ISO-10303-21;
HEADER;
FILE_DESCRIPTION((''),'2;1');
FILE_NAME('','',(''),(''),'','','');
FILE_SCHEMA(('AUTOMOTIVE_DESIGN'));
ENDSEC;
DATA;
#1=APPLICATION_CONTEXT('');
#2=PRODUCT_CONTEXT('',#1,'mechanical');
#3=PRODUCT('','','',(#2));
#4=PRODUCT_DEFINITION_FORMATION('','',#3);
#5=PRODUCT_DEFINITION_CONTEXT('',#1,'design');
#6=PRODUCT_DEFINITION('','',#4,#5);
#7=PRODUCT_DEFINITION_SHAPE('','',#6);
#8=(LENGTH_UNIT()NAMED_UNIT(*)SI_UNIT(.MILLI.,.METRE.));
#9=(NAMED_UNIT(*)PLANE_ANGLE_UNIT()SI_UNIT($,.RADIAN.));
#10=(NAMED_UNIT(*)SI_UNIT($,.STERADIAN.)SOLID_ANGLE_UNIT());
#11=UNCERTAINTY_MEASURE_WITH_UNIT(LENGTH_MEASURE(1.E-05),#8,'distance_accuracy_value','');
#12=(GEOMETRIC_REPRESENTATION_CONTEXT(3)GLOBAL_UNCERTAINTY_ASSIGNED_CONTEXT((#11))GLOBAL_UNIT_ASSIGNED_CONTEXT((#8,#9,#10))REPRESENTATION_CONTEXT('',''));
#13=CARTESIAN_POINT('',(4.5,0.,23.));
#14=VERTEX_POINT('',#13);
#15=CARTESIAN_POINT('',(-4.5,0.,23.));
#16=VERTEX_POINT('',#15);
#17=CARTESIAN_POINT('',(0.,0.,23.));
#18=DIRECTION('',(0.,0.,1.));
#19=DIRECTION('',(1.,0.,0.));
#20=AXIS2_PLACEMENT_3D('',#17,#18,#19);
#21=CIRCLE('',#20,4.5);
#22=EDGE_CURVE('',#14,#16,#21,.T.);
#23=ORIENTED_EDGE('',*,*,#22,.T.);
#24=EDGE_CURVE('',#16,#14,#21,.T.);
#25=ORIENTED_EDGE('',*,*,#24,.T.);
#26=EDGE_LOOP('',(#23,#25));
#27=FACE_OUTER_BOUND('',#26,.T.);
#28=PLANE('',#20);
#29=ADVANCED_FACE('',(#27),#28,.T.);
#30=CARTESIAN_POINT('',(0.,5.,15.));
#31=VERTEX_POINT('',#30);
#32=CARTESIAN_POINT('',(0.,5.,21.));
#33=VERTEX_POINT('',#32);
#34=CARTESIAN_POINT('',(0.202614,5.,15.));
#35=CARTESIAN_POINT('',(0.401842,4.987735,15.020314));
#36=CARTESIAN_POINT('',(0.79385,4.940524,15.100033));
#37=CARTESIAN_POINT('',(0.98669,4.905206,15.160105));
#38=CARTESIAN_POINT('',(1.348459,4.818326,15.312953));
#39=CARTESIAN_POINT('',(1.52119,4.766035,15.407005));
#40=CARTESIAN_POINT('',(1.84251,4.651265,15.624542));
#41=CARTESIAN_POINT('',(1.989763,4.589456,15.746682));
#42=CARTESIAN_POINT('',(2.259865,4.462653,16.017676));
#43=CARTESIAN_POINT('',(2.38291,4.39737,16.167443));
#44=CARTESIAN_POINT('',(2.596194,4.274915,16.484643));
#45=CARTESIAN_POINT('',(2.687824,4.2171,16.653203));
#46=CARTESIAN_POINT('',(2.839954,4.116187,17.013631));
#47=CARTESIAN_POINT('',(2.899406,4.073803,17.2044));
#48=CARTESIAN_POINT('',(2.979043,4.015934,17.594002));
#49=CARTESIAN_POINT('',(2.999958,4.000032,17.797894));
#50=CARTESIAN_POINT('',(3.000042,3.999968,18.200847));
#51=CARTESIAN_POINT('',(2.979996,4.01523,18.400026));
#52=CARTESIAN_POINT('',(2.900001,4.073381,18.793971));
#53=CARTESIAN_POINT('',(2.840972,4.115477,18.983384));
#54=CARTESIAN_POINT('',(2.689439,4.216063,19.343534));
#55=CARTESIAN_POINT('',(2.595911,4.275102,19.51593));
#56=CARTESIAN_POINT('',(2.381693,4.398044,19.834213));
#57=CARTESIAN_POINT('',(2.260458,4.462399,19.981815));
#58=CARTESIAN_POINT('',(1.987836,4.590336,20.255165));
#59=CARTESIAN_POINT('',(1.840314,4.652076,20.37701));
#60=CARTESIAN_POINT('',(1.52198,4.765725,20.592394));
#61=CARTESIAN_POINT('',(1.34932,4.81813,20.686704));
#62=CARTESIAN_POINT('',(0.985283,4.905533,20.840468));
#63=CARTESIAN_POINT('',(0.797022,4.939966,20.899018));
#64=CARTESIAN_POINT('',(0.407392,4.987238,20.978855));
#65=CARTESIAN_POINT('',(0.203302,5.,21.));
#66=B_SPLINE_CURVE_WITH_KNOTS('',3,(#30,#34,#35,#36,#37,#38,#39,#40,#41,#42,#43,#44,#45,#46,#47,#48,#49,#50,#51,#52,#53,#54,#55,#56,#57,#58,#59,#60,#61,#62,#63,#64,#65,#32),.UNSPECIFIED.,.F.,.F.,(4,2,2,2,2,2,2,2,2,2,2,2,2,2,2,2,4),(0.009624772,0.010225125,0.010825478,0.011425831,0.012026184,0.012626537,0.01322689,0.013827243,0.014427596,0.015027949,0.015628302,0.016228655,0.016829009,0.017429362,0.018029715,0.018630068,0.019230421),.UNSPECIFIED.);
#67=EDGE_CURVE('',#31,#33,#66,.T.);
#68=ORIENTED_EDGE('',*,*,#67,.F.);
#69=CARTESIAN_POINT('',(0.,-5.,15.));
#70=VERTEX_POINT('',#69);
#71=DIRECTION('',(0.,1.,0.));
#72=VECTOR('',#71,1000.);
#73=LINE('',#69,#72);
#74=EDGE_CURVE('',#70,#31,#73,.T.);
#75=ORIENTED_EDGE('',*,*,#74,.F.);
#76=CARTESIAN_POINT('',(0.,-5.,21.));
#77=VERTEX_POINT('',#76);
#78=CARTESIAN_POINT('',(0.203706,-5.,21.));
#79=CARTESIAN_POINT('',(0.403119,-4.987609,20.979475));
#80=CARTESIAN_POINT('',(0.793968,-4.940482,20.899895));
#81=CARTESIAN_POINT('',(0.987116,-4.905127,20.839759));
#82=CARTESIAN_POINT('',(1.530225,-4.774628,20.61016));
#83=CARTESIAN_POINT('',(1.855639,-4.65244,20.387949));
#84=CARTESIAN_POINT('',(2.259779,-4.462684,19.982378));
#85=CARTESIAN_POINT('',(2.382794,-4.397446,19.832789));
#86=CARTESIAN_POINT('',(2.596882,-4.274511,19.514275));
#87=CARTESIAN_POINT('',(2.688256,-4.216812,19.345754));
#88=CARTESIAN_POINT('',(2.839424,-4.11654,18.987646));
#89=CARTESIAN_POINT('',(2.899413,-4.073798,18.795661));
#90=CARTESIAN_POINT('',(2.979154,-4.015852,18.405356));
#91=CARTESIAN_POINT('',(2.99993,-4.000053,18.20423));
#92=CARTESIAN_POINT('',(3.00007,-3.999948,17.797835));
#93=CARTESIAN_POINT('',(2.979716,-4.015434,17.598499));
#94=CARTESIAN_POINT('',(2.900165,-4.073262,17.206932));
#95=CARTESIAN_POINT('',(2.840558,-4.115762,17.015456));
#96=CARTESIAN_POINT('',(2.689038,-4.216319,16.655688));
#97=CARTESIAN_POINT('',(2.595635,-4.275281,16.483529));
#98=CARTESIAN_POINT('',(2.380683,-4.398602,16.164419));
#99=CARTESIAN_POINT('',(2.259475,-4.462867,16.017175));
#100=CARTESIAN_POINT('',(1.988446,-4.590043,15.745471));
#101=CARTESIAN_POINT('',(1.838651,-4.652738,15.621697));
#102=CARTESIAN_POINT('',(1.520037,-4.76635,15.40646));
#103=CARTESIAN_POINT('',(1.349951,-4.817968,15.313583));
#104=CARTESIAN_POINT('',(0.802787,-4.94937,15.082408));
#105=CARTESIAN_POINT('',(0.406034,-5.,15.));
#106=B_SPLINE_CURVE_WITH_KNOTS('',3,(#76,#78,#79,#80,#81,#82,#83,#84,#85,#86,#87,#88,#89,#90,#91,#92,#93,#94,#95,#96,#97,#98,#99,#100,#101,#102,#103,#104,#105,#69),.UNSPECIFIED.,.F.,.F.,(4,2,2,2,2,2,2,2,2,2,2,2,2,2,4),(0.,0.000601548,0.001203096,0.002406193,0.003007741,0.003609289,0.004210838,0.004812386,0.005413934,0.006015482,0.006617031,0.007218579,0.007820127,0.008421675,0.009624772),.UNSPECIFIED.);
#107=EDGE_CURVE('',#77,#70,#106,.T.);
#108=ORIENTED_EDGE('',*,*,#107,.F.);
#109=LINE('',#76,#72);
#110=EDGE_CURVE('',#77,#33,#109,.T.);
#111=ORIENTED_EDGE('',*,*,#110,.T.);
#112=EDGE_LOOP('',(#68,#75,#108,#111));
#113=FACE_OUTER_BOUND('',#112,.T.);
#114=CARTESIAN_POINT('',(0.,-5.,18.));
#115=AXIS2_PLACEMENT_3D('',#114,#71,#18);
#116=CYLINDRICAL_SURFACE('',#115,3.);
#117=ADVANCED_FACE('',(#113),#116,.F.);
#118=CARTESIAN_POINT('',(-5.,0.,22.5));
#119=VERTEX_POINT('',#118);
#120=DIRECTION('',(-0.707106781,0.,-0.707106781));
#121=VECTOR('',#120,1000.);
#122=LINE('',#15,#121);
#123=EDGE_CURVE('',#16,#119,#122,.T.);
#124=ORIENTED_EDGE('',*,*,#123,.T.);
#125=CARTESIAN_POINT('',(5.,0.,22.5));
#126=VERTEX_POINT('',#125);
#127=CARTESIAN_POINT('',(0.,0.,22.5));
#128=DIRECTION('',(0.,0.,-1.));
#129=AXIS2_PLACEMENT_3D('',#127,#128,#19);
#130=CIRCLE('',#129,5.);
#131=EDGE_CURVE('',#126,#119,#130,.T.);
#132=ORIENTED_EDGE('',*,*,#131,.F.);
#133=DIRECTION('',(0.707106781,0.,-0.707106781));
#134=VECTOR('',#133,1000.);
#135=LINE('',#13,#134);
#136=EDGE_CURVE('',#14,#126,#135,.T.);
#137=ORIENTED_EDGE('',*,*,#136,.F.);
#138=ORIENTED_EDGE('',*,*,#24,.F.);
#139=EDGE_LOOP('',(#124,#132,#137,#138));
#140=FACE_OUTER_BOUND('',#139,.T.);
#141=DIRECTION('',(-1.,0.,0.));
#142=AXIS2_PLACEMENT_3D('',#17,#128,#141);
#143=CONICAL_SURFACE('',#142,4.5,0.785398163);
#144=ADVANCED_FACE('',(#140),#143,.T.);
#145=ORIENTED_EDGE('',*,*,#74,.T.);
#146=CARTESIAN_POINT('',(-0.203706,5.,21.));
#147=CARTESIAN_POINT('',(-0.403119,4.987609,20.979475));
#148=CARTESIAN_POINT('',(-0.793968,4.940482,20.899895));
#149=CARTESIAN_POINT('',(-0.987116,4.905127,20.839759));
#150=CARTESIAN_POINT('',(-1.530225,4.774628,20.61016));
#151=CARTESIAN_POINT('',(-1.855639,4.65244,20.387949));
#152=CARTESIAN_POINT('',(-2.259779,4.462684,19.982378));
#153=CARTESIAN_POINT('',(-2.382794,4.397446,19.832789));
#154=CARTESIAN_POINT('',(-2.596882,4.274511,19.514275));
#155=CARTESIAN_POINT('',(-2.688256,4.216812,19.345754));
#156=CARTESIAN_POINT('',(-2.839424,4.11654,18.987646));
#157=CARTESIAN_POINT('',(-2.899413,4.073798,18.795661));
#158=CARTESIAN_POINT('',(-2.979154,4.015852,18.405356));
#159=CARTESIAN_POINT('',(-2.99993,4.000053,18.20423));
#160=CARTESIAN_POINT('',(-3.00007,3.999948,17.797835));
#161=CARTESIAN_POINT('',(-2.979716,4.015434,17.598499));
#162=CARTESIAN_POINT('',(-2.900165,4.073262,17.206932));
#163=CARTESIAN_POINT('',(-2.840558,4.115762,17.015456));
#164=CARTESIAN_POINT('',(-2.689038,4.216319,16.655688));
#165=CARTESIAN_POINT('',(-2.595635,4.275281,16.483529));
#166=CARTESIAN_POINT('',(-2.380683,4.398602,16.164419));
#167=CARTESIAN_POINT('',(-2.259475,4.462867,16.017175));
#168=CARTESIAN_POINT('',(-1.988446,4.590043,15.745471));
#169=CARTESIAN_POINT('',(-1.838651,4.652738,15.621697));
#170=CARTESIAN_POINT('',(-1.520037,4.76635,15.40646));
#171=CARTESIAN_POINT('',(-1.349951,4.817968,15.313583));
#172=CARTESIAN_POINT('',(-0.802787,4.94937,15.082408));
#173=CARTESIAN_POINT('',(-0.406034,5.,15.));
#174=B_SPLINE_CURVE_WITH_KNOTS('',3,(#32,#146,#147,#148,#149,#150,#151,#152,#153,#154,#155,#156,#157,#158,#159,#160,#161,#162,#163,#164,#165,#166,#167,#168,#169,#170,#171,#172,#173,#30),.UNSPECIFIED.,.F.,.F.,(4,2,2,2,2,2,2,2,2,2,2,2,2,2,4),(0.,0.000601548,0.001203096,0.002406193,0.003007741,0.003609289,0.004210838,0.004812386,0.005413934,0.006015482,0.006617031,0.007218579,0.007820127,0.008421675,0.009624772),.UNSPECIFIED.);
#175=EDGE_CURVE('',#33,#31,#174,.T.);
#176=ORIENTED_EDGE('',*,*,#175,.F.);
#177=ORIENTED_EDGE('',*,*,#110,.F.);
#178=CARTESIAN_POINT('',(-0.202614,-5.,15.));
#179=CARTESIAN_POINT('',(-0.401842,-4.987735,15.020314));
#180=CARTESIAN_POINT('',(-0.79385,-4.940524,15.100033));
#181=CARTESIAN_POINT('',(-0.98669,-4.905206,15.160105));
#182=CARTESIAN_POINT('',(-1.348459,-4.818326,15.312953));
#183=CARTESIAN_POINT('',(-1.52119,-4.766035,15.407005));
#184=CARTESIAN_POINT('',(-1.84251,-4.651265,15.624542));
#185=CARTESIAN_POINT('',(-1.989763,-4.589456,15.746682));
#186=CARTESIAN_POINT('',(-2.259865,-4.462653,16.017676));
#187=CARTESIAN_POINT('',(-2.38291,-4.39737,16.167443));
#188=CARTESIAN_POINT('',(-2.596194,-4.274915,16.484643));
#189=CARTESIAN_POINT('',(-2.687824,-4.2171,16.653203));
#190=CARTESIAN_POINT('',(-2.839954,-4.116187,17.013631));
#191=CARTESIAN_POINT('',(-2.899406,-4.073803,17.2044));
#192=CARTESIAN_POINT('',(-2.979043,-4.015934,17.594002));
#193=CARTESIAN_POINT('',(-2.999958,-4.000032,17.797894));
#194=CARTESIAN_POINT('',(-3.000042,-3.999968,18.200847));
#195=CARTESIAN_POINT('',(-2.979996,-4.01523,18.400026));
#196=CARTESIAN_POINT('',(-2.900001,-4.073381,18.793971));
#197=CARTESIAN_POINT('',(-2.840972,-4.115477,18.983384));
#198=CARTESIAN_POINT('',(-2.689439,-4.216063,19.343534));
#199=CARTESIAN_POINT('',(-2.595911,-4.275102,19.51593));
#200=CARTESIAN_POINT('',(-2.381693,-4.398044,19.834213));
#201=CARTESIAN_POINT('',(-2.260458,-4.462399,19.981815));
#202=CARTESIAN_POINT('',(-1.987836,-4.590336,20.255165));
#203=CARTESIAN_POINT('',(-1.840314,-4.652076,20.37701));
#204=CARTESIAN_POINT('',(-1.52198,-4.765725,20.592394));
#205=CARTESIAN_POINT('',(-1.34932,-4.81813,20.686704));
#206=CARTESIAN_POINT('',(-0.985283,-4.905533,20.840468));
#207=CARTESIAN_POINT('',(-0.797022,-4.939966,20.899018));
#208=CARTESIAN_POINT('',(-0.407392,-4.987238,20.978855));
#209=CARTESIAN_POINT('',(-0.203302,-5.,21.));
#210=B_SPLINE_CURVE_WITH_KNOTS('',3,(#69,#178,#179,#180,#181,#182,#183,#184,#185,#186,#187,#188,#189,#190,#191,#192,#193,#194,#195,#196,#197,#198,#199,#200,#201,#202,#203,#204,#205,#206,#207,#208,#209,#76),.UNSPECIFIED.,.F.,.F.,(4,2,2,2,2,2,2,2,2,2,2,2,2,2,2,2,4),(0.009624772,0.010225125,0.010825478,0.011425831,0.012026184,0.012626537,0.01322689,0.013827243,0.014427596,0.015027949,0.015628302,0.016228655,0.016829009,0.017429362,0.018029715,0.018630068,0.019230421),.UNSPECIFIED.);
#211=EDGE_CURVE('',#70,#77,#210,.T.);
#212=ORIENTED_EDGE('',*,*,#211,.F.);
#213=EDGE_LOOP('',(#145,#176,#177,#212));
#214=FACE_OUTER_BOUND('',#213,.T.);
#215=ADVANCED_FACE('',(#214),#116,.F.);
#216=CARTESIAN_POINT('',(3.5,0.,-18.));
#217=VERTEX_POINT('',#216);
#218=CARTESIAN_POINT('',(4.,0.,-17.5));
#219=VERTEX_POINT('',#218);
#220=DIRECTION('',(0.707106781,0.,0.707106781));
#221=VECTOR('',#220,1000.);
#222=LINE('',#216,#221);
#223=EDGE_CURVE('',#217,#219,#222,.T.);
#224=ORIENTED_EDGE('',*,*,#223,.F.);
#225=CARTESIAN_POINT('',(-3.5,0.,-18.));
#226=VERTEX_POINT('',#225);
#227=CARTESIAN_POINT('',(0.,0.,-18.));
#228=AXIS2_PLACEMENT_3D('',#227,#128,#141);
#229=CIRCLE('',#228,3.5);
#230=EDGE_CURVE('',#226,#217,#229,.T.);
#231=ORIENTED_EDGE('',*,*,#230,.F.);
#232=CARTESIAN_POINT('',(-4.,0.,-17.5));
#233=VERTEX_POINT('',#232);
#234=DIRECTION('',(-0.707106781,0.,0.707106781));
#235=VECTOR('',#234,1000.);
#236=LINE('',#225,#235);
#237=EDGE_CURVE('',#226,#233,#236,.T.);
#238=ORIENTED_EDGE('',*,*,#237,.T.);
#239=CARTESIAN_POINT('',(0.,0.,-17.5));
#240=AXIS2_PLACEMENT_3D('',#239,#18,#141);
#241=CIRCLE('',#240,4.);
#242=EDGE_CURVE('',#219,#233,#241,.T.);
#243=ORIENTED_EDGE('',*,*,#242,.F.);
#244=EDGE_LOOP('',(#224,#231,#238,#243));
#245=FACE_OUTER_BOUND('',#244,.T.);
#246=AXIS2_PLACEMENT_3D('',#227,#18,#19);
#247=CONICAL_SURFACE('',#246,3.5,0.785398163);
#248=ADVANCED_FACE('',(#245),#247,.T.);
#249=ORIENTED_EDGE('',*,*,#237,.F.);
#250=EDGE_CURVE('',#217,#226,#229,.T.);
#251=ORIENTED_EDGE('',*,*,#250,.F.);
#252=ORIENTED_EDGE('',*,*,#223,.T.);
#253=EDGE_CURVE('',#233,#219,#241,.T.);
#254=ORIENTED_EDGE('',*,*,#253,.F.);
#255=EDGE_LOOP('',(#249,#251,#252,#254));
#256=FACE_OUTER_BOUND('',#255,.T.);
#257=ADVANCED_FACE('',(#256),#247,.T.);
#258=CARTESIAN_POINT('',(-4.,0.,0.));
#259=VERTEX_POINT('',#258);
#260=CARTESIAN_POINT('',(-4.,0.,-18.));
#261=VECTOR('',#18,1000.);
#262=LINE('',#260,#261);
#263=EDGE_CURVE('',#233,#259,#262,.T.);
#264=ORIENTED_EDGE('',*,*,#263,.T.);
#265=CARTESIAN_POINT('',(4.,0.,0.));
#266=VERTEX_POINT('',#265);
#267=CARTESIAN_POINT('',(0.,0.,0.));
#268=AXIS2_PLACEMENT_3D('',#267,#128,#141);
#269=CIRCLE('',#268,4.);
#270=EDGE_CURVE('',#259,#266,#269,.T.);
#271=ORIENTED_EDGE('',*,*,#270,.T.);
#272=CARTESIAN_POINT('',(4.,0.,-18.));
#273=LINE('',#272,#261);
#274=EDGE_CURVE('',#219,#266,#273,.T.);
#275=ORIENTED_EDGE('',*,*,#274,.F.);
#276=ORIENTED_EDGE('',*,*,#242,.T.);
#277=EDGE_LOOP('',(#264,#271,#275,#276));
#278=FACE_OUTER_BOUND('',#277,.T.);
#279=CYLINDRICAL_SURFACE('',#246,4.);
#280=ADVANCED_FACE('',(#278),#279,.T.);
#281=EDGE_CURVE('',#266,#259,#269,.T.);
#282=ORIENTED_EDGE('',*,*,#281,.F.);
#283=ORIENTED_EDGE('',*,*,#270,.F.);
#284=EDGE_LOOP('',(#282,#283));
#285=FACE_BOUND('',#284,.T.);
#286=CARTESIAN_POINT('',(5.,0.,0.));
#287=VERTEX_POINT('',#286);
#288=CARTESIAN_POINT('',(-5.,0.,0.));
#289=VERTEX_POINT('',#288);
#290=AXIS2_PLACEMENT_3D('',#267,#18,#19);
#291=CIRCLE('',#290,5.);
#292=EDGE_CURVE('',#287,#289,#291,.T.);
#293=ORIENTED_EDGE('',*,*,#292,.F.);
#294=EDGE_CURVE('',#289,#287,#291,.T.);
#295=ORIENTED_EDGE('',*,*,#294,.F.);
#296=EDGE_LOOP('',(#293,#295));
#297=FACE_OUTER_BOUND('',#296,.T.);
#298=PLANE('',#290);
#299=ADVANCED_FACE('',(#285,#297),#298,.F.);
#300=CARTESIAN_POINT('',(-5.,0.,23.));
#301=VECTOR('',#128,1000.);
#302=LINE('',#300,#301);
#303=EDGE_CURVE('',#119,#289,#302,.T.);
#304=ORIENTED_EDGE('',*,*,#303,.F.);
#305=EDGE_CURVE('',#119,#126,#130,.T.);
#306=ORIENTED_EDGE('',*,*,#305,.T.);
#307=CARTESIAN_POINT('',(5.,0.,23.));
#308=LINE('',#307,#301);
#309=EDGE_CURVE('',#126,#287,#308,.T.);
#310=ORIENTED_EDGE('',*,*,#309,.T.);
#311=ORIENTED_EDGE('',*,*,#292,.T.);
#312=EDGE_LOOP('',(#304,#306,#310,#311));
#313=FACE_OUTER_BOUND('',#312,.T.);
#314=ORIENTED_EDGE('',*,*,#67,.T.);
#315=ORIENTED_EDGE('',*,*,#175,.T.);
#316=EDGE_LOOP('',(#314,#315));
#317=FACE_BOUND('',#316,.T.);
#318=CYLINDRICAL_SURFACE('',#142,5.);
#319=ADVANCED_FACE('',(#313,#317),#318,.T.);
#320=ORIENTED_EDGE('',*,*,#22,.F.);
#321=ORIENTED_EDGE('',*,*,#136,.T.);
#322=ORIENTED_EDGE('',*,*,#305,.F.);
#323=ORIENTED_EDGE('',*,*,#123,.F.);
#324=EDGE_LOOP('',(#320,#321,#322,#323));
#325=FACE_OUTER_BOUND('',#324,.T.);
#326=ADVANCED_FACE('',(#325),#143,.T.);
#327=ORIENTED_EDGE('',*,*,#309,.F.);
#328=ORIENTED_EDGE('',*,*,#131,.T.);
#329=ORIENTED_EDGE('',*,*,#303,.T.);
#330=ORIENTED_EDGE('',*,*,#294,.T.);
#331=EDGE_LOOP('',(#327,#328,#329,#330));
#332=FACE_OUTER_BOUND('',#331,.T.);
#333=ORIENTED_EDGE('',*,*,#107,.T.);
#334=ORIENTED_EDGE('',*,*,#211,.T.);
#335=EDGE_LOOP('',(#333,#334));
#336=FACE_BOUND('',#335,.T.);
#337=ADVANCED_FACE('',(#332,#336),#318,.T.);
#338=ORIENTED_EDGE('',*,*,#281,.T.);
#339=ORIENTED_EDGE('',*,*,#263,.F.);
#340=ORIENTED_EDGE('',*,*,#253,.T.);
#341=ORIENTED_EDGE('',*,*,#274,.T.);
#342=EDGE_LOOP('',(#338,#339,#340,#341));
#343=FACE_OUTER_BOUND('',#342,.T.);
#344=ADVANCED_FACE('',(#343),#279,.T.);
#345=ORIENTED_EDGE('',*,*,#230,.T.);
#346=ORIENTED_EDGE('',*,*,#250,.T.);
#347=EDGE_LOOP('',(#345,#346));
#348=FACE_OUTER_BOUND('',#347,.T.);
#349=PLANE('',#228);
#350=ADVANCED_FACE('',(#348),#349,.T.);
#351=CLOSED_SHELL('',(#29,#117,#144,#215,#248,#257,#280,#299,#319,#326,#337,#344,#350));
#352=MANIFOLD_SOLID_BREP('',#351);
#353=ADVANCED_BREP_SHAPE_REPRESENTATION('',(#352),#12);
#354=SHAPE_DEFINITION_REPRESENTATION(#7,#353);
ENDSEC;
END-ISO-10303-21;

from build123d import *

# Parameters (mm, degrees)
SKETCH1_R               = 5
BOSS_EXTRUDE1_DEPTH     = 23
SKETCH2_R               = 4
BOSS_EXTRUDE2_DEPTH     = 18
CHAMFER1_SIZE           = 0.5
CUT_EXTRUDE1_DEPTH      = 25.062418831
CUT_EXTRUDE1_DEPTH_BACK = 25.062418831
SKETCH3_R               = 3


with BuildPart() as part:
    # Sketch1 → Boss-Extrude1 (new body)
    with BuildSketch(Plane.XY):
        Circle(SKETCH1_R)
    extrude(amount=BOSS_EXTRUDE1_DEPTH)

    # Sketch2 → Boss-Extrude2 (add)
    with BuildSketch(Plane(origin=(0, 0, 0), x_dir=(-1, 0, 0), z_dir=(0, 0, -1))):
        Circle(SKETCH2_R)
    extrude(amount=BOSS_EXTRUDE2_DEPTH)

    # Chamfer1
    chamfer1_edges = [part.edges().sort_by_distance(p)[0] for p in [
        (-5, 0, 23),
        (4, 0, -18),
    ]]
    chamfer(chamfer1_edges, length=CHAMFER1_SIZE)

    # Sketch3 → Cut-Extrude1 (cut, two sides: drawn at the far end of the back side and taken through both)
    with BuildSketch(Plane(origin=(0, 0, 0), x_dir=(1, 0, 0), z_dir=(0, 1, 0)).offset(-CUT_EXTRUDE1_DEPTH_BACK)):
        with Locations(Location((0, -18, 0), (0, 0, 270))):
            Circle(SKETCH3_R)
    extrude(amount=CUT_EXTRUDE1_DEPTH + CUT_EXTRUDE1_DEPTH_BACK, mode=Mode.SUBTRACT)


solid = part.part
